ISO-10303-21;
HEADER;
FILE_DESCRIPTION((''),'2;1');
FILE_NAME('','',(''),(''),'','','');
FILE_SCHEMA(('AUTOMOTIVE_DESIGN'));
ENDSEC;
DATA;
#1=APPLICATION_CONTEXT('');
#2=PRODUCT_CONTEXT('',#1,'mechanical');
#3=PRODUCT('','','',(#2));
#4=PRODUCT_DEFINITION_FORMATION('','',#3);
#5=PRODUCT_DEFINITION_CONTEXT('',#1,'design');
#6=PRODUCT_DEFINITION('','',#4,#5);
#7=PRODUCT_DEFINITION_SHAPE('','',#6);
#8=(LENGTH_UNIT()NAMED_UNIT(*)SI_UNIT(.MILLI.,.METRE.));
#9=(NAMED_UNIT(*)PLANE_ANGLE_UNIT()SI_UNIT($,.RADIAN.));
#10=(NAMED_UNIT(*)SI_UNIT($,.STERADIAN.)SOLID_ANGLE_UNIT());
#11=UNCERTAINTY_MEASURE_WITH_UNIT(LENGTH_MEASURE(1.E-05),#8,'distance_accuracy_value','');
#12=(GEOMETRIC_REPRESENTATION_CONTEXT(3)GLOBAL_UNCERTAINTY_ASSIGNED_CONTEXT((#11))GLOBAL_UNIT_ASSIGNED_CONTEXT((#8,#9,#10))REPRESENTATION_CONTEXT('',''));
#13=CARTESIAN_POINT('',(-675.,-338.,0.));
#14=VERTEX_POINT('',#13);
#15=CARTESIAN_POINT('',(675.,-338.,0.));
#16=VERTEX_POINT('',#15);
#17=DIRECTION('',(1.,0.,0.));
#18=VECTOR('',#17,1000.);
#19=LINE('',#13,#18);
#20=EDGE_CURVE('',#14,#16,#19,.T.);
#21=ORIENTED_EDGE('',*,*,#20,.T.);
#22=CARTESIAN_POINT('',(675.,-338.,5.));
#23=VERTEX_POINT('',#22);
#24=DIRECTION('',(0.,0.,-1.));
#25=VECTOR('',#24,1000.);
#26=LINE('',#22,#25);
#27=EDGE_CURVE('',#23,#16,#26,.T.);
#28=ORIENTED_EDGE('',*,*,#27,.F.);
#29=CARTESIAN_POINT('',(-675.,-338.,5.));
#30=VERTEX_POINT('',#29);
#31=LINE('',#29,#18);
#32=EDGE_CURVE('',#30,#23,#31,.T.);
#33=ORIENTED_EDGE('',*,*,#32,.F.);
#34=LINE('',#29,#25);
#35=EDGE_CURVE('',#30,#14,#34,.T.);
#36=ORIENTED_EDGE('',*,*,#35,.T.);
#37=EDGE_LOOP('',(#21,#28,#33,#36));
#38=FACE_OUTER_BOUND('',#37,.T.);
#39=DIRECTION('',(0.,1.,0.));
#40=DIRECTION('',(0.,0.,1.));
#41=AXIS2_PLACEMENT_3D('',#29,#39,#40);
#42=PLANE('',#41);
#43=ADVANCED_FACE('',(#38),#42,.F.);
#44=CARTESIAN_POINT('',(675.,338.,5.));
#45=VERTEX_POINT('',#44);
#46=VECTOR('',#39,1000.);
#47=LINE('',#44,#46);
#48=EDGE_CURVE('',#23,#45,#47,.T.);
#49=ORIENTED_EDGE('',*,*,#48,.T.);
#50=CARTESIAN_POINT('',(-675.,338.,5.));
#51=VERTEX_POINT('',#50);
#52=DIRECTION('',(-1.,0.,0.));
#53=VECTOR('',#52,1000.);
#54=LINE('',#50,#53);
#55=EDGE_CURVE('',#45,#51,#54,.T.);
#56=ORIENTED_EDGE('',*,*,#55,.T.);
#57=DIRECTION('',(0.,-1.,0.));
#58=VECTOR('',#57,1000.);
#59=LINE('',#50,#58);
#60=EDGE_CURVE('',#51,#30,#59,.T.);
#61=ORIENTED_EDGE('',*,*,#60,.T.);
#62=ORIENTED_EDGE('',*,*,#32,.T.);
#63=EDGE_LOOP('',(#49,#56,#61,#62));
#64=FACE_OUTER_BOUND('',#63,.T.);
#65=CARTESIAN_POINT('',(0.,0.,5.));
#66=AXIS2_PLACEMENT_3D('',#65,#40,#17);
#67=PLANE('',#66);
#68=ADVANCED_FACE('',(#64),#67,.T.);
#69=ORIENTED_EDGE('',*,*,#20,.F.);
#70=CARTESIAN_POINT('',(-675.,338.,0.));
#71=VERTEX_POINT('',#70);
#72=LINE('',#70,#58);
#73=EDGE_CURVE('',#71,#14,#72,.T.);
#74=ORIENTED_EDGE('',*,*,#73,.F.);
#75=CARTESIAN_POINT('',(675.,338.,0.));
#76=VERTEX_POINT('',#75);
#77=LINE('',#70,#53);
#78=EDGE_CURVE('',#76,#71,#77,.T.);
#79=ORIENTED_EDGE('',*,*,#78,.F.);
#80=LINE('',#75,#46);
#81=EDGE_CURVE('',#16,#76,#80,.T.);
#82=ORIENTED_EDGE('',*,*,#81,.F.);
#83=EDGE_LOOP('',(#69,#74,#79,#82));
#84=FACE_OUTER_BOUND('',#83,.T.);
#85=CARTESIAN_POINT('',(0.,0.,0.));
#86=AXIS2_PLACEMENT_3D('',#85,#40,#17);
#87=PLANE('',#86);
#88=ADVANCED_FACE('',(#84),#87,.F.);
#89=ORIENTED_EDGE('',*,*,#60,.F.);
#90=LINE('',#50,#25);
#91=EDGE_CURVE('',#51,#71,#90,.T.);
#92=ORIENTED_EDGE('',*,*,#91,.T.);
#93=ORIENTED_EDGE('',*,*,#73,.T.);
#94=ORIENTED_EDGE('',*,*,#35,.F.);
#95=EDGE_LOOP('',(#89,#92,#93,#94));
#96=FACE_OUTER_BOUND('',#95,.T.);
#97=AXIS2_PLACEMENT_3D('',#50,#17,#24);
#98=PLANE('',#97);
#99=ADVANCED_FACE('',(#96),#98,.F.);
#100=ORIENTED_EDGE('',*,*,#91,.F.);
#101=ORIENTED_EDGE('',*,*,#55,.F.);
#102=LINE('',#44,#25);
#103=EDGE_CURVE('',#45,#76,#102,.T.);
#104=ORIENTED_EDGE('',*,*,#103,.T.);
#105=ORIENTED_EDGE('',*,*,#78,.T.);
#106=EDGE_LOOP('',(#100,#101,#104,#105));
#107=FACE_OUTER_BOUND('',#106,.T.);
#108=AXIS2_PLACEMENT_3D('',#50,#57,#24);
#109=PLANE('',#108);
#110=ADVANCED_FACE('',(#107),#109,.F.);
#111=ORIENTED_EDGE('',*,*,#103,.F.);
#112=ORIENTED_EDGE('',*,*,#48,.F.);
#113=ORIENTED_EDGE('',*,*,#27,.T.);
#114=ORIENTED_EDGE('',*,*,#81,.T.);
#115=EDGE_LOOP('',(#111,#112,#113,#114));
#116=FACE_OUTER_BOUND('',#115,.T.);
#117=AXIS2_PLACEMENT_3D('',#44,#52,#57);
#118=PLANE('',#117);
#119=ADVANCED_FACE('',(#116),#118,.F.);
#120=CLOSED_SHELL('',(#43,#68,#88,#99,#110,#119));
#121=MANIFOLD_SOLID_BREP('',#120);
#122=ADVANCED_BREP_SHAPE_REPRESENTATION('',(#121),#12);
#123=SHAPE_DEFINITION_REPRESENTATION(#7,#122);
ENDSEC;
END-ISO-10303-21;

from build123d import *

# Parameters (mm, degrees)
SKETCH_1_W      = 1350
SKETCH_1_H      = 676
EXTRUDE_1_DEPTH = 5


with BuildPart() as part:
    # 草图1 → 凸台-拉伸1 (new body)
    with BuildSketch(Plane.XY):
        Rectangle(SKETCH_1_W, SKETCH_1_H)
    extrude(amount=EXTRUDE_1_DEPTH)


solid = part.part
